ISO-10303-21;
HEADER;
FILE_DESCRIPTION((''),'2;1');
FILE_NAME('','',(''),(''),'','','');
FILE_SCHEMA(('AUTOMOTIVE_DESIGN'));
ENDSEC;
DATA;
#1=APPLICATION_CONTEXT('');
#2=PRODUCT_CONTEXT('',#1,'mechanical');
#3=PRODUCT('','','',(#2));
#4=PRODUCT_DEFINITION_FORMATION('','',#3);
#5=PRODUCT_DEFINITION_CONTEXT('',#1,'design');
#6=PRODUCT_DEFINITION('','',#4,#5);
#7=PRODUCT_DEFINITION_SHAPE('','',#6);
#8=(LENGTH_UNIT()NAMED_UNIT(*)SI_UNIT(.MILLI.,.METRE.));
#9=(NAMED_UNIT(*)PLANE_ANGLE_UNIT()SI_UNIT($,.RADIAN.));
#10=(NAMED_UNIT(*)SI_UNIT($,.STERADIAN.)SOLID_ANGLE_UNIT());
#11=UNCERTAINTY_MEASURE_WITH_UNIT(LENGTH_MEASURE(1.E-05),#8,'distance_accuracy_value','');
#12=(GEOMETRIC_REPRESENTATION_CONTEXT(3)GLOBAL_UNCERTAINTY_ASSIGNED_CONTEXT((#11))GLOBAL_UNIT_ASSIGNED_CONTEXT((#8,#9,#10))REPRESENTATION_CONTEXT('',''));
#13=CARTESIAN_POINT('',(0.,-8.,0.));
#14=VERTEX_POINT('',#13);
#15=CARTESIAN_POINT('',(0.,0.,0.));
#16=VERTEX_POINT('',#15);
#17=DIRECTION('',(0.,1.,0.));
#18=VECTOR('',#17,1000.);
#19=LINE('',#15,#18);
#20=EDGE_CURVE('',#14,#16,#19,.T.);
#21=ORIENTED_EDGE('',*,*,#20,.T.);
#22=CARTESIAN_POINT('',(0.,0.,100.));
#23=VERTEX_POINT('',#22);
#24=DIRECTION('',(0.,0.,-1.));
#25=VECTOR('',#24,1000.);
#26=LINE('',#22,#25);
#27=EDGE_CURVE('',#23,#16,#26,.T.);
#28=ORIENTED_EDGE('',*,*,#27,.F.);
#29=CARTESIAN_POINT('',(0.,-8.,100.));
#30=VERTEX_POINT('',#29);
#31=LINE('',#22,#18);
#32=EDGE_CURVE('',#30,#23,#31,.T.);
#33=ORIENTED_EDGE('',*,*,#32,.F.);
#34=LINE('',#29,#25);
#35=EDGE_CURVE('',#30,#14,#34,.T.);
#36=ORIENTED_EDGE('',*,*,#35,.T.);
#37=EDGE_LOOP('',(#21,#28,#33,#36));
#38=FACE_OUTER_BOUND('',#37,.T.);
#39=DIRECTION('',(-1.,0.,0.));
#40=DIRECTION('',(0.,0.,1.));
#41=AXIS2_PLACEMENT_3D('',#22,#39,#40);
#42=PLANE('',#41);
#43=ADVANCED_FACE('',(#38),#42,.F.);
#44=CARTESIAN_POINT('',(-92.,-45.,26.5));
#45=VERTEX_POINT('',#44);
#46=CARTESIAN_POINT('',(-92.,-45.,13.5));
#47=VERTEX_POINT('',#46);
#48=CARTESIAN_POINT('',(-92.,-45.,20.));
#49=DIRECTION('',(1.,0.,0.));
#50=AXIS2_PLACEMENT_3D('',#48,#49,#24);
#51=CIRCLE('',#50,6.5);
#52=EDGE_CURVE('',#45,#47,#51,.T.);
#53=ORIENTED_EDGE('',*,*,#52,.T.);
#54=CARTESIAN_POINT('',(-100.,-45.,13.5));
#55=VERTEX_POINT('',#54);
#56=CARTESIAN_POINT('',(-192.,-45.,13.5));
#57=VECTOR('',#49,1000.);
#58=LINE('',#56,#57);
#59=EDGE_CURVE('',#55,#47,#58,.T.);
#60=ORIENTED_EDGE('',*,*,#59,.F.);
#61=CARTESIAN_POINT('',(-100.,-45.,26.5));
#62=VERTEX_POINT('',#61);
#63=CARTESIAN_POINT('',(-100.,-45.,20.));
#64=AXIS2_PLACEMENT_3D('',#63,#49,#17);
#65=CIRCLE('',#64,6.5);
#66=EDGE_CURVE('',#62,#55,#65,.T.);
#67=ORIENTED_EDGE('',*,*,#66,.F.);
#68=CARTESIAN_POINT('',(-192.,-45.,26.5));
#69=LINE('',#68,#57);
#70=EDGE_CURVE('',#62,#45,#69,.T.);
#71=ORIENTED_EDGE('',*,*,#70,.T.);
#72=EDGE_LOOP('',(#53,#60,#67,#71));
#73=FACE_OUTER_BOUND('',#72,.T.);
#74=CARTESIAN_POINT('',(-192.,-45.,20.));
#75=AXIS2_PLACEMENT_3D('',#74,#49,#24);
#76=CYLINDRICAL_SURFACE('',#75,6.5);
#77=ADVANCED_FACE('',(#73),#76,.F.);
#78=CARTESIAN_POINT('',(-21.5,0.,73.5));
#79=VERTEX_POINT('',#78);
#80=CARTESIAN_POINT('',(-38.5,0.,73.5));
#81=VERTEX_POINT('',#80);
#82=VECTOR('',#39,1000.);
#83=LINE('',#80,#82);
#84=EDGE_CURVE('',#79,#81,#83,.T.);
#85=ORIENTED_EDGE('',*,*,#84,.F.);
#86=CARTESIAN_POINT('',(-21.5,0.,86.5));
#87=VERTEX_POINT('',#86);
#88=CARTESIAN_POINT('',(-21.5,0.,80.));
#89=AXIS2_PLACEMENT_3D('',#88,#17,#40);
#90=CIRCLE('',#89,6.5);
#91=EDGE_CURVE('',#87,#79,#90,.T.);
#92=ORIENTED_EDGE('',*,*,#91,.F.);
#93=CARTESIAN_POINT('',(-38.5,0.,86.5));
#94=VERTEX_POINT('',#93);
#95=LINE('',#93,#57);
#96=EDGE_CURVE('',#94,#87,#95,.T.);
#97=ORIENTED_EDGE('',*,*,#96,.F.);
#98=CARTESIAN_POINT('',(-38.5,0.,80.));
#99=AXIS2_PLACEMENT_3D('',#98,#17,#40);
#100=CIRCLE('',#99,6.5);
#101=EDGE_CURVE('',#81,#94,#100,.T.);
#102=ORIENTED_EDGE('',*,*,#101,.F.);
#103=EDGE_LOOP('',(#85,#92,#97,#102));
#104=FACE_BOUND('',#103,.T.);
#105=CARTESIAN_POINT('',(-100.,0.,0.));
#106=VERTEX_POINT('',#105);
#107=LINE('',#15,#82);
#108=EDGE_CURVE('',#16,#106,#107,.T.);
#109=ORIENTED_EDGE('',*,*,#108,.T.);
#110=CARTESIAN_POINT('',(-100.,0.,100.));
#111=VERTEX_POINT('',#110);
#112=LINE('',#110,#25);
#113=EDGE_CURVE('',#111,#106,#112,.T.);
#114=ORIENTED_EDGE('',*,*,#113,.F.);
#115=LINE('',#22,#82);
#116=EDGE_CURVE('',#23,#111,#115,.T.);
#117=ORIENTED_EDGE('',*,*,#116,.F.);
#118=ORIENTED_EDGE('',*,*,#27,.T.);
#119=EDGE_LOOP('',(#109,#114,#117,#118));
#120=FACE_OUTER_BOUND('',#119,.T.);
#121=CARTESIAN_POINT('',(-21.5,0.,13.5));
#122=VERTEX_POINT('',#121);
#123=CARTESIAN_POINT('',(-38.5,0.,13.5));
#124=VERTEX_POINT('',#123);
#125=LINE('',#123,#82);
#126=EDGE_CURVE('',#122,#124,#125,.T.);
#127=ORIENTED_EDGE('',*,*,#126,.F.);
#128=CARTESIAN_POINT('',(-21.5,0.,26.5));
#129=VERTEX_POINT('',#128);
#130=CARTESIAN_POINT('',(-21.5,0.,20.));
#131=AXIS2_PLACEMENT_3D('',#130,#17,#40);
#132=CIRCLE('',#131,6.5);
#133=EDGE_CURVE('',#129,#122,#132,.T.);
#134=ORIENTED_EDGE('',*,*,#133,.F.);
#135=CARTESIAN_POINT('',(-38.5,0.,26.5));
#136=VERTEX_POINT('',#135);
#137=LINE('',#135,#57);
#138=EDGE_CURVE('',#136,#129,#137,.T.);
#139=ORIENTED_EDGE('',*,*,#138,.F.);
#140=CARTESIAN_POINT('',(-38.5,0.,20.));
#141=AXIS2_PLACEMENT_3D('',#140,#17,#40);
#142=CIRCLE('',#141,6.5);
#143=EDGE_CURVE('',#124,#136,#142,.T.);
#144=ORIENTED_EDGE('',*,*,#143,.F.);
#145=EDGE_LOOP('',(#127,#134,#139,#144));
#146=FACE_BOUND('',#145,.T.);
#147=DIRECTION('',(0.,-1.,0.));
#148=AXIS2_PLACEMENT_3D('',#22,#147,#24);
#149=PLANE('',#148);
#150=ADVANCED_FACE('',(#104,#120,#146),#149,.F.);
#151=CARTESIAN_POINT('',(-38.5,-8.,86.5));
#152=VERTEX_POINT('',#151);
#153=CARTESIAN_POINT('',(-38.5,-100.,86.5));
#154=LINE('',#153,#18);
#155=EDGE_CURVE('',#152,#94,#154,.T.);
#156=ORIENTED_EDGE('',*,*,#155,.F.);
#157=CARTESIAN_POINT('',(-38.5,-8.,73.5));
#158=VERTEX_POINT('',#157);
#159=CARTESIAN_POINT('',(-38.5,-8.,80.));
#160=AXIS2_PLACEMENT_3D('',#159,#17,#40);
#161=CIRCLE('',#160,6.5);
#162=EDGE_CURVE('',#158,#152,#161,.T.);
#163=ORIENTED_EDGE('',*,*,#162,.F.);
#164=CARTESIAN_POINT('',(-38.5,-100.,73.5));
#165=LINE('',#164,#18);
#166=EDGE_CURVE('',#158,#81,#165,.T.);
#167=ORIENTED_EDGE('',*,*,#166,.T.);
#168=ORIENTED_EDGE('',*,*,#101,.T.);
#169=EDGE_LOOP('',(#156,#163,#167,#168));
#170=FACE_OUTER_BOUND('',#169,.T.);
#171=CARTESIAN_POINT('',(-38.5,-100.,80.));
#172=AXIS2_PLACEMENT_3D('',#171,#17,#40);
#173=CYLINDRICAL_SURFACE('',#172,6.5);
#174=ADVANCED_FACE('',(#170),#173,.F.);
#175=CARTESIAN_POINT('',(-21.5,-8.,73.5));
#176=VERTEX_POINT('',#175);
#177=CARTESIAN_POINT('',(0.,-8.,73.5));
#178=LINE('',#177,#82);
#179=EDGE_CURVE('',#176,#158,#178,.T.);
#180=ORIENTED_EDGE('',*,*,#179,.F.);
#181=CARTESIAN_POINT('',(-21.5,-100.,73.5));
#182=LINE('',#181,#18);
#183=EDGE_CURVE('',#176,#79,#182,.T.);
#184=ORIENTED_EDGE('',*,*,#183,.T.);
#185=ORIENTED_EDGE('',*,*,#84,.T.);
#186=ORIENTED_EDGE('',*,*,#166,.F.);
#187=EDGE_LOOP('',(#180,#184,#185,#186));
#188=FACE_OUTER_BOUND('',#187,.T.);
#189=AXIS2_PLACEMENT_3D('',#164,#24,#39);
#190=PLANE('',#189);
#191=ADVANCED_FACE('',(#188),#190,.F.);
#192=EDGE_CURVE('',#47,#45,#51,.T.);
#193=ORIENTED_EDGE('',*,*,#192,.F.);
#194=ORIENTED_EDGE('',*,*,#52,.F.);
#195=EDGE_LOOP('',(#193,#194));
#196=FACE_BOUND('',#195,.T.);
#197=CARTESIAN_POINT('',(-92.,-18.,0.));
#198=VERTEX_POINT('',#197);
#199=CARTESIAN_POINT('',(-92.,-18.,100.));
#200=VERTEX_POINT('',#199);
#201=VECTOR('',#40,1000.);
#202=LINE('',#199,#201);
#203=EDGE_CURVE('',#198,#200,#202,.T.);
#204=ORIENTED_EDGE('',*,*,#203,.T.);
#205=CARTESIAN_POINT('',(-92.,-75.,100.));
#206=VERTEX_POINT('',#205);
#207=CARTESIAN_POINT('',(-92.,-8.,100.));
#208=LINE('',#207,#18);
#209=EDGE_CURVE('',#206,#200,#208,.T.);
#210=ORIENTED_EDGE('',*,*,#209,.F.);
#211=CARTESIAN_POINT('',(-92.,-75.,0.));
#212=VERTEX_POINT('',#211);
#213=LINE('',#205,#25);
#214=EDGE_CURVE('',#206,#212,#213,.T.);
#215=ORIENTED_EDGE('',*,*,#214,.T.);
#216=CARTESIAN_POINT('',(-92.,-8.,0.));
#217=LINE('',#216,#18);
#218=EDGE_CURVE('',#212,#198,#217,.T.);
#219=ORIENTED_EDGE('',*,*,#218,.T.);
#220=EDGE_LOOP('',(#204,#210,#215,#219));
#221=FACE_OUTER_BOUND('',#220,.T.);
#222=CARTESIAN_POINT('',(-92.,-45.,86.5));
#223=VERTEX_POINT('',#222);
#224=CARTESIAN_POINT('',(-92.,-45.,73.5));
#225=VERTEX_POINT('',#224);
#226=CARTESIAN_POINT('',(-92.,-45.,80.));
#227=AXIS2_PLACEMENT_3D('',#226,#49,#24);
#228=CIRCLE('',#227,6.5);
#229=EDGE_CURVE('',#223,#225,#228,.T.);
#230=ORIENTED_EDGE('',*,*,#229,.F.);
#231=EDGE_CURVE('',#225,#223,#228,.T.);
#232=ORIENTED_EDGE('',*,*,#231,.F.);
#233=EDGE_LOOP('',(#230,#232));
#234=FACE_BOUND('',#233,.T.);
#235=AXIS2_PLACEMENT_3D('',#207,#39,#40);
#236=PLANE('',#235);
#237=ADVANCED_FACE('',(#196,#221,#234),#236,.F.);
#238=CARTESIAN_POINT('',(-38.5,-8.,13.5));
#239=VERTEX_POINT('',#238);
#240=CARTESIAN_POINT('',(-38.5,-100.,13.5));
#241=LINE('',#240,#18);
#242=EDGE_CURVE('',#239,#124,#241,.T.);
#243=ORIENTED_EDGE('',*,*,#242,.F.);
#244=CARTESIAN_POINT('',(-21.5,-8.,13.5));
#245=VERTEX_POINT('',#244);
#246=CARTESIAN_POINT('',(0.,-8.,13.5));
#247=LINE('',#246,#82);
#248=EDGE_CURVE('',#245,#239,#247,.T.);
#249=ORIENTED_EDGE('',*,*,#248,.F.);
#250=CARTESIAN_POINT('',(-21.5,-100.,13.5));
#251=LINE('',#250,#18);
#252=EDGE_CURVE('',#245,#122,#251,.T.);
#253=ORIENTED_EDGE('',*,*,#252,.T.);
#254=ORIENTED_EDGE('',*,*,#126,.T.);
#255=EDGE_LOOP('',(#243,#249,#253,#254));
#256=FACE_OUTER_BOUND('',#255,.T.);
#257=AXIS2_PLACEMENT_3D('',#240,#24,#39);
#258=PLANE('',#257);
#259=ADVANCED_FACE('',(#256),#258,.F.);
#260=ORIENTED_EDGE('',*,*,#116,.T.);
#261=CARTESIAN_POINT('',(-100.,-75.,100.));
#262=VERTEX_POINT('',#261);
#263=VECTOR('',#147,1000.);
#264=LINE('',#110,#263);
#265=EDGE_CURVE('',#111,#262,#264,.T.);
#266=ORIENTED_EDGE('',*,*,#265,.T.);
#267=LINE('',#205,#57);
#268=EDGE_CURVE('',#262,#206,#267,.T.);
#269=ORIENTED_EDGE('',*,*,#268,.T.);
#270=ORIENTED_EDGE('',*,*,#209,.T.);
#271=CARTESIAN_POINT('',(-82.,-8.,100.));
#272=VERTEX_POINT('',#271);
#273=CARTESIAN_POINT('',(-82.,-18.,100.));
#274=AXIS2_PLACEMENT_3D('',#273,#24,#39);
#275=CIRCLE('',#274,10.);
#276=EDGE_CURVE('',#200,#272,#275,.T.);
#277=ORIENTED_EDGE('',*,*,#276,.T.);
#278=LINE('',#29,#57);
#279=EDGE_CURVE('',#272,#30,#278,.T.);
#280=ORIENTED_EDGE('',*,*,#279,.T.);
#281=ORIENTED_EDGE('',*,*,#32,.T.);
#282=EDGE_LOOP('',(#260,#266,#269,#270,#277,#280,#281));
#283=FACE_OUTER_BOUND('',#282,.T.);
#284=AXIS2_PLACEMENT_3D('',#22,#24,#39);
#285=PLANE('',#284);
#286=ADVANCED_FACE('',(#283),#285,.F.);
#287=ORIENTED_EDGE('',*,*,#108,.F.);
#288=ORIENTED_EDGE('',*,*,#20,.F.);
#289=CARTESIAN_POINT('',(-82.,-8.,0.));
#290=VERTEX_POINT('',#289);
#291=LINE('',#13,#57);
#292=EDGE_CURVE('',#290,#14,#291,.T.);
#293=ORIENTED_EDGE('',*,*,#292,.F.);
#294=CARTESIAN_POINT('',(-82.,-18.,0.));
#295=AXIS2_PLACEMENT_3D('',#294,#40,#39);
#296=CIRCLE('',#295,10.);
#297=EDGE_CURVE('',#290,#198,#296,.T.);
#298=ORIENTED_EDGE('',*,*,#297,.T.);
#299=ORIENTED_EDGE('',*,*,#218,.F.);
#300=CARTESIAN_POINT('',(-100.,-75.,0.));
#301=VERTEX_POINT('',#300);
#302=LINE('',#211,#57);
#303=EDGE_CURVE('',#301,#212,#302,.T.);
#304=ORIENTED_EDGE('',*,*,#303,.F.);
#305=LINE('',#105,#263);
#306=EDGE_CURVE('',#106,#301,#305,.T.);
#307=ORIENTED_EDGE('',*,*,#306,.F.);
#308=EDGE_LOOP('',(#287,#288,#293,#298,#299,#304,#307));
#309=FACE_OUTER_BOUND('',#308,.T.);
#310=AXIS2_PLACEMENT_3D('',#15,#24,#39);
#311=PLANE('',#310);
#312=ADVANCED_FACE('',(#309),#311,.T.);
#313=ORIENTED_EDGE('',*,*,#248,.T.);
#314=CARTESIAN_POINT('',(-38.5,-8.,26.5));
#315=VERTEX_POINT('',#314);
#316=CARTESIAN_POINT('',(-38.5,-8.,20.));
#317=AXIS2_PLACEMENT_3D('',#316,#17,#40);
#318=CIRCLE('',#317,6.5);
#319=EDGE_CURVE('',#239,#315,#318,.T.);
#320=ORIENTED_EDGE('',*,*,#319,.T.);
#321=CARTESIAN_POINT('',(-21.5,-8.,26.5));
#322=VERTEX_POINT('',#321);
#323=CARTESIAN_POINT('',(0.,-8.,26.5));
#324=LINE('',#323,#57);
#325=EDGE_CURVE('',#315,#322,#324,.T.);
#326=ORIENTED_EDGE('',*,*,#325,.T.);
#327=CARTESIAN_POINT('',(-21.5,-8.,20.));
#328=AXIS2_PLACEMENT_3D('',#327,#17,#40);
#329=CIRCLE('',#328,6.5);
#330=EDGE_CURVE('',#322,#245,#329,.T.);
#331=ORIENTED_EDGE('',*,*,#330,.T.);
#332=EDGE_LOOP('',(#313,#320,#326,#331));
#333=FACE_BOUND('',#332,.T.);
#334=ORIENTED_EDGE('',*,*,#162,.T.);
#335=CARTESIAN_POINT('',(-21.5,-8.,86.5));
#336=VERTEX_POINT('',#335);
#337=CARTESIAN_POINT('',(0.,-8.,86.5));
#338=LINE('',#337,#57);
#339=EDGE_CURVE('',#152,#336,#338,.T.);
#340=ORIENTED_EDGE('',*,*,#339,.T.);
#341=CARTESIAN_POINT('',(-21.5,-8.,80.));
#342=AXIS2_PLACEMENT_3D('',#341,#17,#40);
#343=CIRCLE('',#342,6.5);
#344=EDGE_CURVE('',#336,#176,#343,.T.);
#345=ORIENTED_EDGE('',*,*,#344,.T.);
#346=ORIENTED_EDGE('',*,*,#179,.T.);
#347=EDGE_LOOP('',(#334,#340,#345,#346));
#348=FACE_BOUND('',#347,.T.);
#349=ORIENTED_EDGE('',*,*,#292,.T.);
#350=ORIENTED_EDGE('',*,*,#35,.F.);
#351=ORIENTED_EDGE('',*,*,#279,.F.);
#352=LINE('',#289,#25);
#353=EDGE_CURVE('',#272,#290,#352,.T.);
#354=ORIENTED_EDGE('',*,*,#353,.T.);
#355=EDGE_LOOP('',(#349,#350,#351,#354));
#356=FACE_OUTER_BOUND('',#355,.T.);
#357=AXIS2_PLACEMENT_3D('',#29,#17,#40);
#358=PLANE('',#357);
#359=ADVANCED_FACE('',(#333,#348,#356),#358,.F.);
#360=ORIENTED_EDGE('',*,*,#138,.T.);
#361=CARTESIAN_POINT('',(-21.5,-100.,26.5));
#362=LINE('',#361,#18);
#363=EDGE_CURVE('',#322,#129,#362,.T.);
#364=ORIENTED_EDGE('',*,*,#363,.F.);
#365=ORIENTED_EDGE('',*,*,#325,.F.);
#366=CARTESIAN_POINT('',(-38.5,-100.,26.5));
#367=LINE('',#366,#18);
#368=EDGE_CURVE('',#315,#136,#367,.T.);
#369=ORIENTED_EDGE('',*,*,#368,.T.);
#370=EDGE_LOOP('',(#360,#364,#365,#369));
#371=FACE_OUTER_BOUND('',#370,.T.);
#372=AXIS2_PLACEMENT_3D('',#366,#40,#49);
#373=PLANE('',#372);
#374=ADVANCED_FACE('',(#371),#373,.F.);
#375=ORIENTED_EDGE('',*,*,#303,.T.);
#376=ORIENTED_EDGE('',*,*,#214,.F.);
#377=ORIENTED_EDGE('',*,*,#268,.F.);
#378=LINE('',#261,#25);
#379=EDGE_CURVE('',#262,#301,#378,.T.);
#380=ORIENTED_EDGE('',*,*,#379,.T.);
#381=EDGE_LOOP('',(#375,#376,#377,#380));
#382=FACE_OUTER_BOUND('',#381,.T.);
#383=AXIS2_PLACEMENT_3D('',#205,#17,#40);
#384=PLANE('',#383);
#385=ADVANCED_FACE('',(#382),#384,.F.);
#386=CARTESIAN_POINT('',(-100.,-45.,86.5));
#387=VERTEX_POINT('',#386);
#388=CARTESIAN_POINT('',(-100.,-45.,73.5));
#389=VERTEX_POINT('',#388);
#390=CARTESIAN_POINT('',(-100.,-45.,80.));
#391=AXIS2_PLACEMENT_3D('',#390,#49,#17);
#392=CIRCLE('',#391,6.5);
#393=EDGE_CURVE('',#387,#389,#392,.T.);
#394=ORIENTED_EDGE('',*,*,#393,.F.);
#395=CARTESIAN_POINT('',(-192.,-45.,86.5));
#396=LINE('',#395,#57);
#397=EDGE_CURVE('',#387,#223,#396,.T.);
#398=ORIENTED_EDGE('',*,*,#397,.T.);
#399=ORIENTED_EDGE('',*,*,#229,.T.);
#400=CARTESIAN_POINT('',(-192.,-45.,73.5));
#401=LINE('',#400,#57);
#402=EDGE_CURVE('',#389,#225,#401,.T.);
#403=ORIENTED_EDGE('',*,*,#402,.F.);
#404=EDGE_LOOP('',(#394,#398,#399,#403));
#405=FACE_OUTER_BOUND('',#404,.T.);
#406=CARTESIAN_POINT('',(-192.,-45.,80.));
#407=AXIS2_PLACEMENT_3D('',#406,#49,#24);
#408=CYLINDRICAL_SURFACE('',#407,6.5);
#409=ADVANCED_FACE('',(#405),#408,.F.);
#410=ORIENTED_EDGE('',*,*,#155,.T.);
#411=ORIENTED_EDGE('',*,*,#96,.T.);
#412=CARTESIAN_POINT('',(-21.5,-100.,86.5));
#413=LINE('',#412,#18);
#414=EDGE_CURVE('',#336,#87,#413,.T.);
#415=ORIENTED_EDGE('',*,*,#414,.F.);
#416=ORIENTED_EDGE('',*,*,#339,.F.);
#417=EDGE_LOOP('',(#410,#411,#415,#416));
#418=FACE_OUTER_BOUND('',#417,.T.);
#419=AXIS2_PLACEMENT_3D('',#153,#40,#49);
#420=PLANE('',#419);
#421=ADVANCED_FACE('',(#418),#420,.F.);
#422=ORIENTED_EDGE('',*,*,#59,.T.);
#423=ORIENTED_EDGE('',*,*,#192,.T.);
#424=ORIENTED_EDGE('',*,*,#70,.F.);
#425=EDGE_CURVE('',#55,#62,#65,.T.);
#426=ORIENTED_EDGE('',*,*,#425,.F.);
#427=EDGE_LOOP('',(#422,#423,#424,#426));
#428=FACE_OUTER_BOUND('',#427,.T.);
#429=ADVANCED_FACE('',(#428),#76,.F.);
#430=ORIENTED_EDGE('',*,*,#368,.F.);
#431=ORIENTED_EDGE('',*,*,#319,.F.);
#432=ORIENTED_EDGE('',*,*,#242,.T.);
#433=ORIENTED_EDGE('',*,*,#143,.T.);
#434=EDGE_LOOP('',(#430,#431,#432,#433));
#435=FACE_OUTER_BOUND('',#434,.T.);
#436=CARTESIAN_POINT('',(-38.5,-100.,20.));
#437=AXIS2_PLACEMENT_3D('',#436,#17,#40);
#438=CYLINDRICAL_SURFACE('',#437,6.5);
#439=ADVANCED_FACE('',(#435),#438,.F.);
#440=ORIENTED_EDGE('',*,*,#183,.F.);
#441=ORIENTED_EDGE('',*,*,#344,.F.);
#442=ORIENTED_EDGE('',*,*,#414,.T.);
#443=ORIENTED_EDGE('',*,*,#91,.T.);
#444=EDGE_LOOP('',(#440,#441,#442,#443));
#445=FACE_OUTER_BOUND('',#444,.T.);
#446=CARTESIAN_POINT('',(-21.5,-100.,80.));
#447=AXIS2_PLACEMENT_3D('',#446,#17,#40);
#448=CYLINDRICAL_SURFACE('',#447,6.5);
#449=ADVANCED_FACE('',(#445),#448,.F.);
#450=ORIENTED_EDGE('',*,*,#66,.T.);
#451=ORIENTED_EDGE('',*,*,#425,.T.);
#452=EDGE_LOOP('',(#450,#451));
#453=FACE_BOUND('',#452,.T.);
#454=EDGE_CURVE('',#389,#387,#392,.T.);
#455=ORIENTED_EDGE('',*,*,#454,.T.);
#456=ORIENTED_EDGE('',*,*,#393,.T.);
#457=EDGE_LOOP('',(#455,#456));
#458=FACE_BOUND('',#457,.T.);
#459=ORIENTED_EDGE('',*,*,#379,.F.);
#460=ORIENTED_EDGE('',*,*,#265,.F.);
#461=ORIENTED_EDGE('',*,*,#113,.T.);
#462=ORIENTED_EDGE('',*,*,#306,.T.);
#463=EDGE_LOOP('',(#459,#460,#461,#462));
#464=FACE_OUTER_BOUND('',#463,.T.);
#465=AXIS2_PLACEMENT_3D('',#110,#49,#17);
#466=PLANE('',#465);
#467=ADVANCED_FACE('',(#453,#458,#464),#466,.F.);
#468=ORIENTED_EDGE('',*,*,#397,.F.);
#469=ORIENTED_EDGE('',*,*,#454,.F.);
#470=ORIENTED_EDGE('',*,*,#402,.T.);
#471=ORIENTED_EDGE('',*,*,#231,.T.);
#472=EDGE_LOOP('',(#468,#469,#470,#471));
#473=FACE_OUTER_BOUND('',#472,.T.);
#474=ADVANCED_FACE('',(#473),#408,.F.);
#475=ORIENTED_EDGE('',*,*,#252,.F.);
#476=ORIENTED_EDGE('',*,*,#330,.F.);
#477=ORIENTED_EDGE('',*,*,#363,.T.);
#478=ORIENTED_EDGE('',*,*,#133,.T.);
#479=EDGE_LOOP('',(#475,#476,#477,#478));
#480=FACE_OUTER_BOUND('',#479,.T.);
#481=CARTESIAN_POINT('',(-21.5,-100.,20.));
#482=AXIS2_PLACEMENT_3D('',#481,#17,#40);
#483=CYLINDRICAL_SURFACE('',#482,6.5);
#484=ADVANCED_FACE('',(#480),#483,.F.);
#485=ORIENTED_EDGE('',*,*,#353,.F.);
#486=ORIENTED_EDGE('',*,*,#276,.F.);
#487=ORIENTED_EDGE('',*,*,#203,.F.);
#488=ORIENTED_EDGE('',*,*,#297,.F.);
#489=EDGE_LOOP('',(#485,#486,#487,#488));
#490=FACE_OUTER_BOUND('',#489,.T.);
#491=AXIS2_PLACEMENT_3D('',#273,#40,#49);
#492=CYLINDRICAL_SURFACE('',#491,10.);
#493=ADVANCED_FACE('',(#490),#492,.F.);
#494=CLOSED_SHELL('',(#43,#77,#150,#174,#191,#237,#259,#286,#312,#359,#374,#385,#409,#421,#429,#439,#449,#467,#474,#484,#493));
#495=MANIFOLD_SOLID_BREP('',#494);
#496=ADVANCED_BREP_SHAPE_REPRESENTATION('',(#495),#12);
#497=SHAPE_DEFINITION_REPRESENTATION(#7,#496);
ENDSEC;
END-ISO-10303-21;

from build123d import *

# Parameters (mm, degrees)
EXTRUDE_1_DEPTH     = 100
CUT_EXTRUDE_1_DEPTH = 100
SKETCH_3_R          = 6.5
CUT_EXTRUDE_2_DEPTH = 100
FILLET_1_R          = 10


with BuildPart() as part:
    # 草图1 → 凸台-拉伸1 (new body)
    with BuildSketch(Plane.XY):
        Polygon((0, 0), (-100, 0), (-100, -75), (-92, -75), (-92, -8), (0, -8), align=None)
    extrude(amount=EXTRUDE_1_DEPTH)

    # 草图2 → 切除-拉伸1 (cut)
    with BuildSketch(Plane(origin=(0, 0, 0), x_dir=(1, 0, 0), z_dir=(0, 1, 0))):
        with BuildLine():
            Line((-38.5, -13.5), (-21.5, -13.5))
            ThreePointArc((-21.5, -13.5), (-15, -20), (-21.5, -26.5))
            Line((-21.5, -26.5), (-38.5, -26.5))
            ThreePointArc((-38.5, -26.5), (-45, -20), (-38.5, -13.5))
        make_face()
        with BuildLine():
            Line((-38.5, -73.5), (-21.5, -73.5))
            ThreePointArc((-21.5, -73.5), (-15, -80), (-21.5, -86.5))
            Line((-21.5, -86.5), (-38.5, -86.5))
            ThreePointArc((-38.5, -86.5), (-45, -80), (-38.5, -73.5))
        make_face()
    extrude(amount=-CUT_EXTRUDE_1_DEPTH, mode=Mode.SUBTRACT)

    # 草图3 → 切除-拉伸2 (cut)
    with BuildSketch(Plane(origin=(-92, 0, 0), x_dir=(0, 0, -1), z_dir=(1, 0, 0))):
        with Locations((-80, -45)):
            Circle(SKETCH_3_R)
        with Locations((-20, -45)):
            Circle(SKETCH_3_R)
    extrude(amount=-CUT_EXTRUDE_2_DEPTH, mode=Mode.SUBTRACT)

    # 圆角1
    fillet_1_edges = [part.edges().sort_by_distance(p)[0] for p in [
        (-92, -8, 50),
    ]]
    fillet(fillet_1_edges, radius=FILLET_1_R)


solid = part.part
